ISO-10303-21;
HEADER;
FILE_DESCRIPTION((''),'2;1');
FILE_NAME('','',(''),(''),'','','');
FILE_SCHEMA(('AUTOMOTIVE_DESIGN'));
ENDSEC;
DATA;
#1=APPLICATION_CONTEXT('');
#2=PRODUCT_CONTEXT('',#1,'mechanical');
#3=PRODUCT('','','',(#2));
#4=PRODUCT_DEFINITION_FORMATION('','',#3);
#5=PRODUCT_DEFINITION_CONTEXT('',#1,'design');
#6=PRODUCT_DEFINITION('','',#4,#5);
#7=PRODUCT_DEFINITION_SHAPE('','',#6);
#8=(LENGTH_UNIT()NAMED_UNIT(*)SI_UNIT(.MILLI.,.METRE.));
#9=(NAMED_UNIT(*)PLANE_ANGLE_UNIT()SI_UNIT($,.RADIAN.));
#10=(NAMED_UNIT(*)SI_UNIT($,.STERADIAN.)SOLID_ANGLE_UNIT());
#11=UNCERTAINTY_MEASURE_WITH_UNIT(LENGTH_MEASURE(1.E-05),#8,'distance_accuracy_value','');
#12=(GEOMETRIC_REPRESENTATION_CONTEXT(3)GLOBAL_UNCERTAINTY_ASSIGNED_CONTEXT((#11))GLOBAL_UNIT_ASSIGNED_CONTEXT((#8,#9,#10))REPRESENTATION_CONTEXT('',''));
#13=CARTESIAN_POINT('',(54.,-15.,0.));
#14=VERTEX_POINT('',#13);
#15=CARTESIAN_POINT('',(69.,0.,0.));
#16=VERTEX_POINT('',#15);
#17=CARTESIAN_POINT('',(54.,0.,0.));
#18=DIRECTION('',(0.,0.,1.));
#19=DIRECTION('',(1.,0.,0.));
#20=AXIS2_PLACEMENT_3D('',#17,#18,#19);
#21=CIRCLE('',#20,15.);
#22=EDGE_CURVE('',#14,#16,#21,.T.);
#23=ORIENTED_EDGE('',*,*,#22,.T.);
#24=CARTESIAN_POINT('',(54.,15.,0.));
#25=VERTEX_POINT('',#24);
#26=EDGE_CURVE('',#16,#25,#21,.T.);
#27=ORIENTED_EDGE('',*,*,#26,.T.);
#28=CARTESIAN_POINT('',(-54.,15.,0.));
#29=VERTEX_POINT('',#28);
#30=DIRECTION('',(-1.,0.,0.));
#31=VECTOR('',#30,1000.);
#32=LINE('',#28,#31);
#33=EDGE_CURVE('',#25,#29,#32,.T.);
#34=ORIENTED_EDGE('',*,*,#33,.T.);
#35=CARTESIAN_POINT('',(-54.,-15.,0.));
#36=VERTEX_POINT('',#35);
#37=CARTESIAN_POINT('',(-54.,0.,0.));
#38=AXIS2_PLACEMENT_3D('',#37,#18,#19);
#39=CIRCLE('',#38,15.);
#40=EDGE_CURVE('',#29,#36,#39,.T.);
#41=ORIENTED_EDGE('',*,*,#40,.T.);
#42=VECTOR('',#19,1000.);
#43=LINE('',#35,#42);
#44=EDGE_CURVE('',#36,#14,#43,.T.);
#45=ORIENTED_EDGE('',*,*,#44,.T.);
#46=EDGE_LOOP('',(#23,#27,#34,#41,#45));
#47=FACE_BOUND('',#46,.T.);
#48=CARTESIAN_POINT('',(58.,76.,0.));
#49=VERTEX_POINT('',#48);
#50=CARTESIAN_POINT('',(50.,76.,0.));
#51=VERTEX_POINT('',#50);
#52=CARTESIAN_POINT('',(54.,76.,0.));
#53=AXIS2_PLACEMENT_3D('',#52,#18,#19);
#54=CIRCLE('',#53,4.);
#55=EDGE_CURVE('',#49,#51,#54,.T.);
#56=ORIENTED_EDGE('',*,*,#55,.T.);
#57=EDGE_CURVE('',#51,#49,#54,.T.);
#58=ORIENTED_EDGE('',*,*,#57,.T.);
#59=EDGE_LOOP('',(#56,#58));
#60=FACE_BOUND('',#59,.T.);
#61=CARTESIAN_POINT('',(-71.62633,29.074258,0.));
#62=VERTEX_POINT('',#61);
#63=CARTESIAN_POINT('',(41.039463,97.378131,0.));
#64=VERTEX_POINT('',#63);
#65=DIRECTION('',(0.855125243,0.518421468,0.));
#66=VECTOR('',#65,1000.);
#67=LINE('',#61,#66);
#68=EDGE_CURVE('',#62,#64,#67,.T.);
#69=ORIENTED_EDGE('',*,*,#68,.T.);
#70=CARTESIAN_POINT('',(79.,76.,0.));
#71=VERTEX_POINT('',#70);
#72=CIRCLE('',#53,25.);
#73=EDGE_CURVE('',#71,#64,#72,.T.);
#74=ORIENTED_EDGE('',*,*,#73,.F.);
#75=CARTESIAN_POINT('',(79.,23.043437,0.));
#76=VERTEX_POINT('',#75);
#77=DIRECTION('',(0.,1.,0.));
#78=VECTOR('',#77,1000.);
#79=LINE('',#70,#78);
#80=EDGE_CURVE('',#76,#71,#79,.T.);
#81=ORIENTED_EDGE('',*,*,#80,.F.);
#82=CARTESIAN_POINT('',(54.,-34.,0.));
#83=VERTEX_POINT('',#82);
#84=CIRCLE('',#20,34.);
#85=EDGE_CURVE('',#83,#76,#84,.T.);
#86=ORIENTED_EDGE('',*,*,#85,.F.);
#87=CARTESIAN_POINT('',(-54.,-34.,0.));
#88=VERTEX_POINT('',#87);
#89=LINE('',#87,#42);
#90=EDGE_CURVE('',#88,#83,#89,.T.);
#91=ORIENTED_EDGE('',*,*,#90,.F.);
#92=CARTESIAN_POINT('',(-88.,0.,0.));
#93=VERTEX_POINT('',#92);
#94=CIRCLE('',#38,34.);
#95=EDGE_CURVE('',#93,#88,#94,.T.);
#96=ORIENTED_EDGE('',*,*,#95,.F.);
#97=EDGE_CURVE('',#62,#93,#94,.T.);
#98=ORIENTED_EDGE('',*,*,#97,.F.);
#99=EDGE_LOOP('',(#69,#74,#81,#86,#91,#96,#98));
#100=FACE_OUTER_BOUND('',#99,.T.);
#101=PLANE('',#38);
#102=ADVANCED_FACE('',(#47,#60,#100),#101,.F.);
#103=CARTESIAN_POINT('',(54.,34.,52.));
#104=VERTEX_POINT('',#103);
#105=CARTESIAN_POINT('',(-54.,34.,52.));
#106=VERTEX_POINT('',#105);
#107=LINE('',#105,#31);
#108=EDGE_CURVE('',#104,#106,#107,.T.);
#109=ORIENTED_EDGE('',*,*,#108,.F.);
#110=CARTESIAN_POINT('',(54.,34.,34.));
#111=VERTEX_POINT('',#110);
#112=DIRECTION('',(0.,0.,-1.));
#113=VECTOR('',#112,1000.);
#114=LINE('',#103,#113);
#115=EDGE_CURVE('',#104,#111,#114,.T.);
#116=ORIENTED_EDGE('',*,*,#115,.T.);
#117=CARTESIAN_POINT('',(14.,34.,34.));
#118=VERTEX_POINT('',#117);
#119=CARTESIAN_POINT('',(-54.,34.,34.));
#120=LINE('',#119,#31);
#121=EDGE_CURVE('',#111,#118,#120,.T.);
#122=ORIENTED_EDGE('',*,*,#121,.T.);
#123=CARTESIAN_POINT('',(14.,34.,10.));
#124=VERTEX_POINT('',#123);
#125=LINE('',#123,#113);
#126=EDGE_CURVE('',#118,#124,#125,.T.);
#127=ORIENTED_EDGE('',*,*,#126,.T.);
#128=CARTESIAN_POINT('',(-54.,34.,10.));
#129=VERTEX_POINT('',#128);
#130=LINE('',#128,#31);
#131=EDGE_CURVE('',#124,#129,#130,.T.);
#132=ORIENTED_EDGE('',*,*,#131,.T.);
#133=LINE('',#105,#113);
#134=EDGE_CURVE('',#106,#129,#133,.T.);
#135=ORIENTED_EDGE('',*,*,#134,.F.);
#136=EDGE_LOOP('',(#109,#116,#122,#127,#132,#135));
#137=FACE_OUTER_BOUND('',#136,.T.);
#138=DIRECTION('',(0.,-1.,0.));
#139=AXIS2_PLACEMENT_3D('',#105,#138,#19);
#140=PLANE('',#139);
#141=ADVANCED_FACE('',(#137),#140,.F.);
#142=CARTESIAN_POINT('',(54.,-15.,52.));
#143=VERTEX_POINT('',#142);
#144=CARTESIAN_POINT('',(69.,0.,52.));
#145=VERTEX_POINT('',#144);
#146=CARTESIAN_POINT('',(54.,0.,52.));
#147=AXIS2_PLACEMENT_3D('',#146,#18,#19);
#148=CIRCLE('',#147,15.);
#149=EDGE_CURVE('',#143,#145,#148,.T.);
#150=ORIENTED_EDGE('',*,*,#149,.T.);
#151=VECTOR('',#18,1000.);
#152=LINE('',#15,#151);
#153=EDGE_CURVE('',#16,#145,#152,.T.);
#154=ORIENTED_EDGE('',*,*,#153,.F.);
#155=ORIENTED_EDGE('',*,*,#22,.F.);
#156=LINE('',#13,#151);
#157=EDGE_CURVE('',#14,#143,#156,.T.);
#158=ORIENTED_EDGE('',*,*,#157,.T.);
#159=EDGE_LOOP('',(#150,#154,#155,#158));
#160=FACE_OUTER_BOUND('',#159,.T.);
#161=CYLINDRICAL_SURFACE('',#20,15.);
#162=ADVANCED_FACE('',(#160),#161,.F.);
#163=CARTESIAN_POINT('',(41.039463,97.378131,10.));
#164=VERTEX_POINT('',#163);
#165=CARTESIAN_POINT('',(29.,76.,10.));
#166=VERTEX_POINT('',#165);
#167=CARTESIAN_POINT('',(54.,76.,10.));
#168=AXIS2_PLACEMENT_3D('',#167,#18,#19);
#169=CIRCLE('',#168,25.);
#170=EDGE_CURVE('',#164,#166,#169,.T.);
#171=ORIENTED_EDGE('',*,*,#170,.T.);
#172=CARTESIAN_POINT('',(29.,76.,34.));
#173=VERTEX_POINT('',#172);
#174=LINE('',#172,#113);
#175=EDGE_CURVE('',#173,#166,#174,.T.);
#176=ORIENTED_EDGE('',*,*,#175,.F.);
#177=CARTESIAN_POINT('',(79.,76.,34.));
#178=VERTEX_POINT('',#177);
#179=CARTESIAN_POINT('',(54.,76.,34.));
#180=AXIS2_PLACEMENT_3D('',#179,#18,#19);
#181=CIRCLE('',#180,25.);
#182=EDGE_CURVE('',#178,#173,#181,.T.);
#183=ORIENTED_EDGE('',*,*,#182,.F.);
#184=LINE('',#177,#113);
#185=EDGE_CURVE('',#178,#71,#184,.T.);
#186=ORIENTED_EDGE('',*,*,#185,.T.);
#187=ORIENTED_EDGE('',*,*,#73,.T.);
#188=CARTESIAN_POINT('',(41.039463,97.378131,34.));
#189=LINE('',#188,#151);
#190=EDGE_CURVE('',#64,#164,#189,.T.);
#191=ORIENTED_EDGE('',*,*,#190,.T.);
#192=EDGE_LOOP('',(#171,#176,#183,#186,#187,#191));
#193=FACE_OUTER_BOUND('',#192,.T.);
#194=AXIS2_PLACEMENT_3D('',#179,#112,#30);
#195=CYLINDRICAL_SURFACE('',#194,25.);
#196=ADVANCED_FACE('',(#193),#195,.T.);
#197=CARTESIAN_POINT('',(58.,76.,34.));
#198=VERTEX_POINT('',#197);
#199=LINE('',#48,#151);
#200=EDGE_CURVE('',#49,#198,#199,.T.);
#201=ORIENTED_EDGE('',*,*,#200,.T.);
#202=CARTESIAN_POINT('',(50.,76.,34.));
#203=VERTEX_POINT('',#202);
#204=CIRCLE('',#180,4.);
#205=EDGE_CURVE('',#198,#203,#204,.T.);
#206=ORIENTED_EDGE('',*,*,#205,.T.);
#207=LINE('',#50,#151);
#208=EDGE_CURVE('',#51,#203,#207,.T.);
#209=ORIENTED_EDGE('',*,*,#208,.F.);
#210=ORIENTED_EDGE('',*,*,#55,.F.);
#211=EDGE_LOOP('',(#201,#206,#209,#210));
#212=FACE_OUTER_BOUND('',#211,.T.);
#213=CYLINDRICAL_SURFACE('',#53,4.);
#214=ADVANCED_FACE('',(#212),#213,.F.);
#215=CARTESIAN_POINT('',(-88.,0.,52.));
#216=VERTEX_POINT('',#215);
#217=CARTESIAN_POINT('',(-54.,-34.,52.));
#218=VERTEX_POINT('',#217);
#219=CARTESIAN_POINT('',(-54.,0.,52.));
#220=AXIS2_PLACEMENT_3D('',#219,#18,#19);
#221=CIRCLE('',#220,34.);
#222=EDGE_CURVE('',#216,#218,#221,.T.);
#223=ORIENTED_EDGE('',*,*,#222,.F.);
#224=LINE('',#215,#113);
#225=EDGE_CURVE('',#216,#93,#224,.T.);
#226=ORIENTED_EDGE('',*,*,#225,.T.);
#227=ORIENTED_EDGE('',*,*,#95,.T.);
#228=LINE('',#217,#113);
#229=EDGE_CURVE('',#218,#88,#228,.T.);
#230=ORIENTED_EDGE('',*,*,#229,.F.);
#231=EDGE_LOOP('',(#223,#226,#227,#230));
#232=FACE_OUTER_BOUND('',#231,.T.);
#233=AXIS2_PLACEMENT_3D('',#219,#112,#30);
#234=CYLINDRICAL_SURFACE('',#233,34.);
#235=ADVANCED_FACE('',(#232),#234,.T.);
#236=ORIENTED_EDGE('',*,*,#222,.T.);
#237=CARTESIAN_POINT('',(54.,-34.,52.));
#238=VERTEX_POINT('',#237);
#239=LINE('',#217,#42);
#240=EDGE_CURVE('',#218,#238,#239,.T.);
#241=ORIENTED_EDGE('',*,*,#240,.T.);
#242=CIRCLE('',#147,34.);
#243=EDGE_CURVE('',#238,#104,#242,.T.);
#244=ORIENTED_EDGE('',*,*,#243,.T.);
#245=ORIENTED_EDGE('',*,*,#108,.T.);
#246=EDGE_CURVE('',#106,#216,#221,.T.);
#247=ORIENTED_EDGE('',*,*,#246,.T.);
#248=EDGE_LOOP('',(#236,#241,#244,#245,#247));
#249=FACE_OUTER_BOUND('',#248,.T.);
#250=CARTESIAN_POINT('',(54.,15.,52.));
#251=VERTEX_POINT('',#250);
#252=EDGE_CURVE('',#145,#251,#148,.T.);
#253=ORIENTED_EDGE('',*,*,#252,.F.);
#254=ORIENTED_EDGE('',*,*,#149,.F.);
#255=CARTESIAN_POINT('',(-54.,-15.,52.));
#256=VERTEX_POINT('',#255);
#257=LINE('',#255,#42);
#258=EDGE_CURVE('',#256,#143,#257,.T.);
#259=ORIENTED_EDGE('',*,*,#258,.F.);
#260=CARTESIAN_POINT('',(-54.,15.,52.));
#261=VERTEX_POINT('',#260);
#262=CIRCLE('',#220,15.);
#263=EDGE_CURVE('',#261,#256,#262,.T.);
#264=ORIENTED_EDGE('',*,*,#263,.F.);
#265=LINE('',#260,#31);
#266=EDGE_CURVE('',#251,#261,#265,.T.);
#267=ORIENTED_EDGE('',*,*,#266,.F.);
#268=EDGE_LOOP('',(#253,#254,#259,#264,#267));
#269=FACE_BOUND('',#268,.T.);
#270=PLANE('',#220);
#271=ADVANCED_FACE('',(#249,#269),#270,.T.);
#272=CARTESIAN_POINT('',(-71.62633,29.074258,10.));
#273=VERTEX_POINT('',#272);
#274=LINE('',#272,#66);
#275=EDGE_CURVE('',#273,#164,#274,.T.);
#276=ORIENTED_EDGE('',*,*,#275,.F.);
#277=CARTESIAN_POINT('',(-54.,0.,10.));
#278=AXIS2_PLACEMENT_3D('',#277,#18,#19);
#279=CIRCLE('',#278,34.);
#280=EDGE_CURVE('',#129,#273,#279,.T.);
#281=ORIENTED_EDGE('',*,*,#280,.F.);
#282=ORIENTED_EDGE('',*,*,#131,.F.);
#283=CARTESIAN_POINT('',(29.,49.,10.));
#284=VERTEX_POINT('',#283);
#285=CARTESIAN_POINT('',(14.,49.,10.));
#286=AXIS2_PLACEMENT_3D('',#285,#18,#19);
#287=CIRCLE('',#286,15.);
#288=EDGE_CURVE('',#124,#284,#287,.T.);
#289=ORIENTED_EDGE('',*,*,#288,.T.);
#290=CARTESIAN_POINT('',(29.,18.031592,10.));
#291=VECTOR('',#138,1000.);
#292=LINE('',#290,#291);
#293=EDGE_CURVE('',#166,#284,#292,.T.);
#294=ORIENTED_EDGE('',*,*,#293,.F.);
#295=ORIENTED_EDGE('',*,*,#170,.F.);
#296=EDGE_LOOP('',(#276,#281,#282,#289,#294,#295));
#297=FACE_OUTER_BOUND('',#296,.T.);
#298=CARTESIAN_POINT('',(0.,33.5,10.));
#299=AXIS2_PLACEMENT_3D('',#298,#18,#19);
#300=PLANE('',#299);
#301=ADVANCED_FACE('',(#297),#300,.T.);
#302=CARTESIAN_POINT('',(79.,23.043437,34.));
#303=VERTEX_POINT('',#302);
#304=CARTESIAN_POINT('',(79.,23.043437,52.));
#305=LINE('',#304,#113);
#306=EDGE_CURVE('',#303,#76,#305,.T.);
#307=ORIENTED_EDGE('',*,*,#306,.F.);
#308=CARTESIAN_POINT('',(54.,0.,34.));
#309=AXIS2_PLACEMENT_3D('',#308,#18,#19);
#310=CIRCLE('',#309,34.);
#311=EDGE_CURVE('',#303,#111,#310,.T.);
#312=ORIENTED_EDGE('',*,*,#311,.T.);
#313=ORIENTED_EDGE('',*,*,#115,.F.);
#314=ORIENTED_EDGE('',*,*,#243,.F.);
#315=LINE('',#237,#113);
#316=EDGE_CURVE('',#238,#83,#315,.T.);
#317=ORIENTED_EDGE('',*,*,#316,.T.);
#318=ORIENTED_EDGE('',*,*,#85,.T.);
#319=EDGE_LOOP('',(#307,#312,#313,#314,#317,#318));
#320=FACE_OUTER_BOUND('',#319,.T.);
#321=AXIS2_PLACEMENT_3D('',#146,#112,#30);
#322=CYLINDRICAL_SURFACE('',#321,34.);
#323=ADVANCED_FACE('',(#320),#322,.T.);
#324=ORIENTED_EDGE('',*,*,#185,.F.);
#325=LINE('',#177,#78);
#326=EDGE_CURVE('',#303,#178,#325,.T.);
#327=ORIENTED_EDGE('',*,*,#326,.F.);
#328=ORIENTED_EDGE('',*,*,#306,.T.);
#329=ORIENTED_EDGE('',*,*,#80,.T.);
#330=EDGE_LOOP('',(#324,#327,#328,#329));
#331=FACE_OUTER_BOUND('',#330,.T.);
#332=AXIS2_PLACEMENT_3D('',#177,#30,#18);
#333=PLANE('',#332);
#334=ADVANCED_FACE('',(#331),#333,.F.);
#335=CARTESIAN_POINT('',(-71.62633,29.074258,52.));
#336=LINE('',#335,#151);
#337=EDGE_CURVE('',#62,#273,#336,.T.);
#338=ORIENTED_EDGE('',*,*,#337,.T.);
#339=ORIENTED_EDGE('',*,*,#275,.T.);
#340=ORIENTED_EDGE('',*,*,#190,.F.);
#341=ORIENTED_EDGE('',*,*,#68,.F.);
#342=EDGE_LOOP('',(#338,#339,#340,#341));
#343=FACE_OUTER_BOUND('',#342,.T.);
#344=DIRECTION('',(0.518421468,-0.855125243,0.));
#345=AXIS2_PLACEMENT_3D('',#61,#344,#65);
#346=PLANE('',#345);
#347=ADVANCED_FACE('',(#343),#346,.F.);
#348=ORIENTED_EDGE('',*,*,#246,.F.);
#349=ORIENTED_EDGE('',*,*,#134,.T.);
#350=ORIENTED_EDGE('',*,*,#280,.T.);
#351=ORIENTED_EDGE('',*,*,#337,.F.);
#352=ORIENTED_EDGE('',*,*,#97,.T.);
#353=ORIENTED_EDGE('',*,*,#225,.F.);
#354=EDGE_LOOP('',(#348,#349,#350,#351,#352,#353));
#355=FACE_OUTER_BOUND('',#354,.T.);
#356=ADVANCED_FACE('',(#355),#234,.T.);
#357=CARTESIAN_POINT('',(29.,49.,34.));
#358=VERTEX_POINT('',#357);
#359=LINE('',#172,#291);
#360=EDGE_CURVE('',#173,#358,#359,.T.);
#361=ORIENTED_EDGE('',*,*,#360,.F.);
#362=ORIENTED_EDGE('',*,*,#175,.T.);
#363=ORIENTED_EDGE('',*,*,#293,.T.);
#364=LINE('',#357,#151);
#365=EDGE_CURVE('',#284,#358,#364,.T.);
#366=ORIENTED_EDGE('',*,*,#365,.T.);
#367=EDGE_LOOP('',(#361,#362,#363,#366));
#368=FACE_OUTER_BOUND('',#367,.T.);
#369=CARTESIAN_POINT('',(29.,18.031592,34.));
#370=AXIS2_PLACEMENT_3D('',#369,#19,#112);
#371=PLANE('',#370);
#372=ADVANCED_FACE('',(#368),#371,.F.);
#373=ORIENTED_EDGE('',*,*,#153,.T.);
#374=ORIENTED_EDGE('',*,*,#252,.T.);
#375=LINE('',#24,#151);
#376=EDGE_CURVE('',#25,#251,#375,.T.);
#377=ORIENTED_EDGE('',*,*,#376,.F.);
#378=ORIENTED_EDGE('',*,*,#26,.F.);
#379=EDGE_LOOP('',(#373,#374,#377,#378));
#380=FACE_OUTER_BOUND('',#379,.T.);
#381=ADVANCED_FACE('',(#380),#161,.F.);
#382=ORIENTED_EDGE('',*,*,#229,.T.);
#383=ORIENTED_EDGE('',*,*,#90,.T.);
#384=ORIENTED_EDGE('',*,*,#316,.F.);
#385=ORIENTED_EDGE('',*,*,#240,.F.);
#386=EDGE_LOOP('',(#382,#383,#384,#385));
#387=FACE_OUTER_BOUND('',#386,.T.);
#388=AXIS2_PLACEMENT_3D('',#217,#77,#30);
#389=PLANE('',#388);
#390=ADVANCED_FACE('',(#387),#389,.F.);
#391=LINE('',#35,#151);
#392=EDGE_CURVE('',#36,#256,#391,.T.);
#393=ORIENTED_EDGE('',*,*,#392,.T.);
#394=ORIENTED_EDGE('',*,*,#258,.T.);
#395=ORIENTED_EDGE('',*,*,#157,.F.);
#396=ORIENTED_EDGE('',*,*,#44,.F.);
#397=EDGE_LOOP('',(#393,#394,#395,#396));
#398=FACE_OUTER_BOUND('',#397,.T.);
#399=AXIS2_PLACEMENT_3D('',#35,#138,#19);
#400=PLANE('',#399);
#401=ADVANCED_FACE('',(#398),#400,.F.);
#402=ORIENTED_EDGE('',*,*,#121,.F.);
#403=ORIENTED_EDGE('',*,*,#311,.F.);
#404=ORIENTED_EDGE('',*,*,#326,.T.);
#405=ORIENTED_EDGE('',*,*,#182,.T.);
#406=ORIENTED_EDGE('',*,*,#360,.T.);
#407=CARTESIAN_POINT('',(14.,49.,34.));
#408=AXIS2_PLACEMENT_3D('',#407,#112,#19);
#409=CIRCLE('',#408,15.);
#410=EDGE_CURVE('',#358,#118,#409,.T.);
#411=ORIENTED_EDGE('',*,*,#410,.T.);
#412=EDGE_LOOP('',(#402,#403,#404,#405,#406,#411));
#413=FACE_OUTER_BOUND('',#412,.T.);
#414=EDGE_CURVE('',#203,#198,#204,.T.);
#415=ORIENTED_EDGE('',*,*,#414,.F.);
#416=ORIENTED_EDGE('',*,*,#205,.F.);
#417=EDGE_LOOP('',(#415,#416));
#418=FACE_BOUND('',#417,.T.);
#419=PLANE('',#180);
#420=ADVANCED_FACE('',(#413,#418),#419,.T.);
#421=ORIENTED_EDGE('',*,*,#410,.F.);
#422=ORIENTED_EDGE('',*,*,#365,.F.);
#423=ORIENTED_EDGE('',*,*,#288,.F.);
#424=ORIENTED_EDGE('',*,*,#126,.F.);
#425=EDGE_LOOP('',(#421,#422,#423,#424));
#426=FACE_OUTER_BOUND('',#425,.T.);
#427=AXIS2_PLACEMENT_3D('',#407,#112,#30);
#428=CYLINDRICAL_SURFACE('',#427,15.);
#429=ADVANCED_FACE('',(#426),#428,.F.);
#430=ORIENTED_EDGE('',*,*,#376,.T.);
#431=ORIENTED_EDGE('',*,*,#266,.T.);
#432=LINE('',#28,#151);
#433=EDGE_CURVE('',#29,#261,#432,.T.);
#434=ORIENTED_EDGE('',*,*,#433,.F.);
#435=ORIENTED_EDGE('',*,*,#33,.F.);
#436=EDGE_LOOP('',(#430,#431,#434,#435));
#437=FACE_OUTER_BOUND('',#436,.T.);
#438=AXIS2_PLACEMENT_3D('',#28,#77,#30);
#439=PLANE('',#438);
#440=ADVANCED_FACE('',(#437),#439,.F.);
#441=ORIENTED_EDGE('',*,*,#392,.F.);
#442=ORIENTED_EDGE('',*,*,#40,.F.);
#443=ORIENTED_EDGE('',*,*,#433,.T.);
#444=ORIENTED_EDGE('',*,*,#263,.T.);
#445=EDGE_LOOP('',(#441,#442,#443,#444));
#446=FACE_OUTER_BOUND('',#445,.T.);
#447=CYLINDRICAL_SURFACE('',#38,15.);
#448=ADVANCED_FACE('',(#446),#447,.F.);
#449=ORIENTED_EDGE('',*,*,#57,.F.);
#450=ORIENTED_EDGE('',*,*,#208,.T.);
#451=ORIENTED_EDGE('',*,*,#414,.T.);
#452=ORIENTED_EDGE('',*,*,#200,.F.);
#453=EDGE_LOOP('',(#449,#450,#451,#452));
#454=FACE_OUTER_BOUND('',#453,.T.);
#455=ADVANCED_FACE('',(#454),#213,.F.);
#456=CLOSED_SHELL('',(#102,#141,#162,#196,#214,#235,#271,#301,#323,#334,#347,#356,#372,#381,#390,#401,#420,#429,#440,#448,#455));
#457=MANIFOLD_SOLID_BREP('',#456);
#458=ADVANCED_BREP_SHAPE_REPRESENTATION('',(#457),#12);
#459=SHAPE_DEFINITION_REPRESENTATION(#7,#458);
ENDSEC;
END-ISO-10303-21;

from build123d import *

# Parameters (mm, degrees)
LINK_PLATE_DEPTH          = 52
LINK_SLOT_DEPTH           = 52
PIVOT_BOSS_DEPTH          = 34
PIVOT_PIN_HOLE_SKETCH_R   = 4
PIVOT_PIN_HOLE_DEPTH      = 34
SUPPORT_RIB_10MM_REACH    = 145.698
SUPPORT_RIB_SKETCH_WALL_W = 421.148756116
SUPPORT_RIB_SKETCH_WALL_H = 10
EDGE_FILLETS_R15_R        = 15


with BuildPart() as part:
    # Link Plate Outline Sketch → Link Plate (new body)
    with BuildSketch(Plane.XY):
        with BuildLine():
            Line((-54, 34), (54, 34))
            ThreePointArc((54, 34), (88, 0), (54, -34))
            Line((54, -34), (-54, -34))
            ThreePointArc((-54, -34), (-88, 0), (-54, 34))
        make_face()
    extrude(amount=LINK_PLATE_DEPTH)

    # Link Slot Sketch → Link Slot (cut)
    with BuildSketch(Plane.XY.offset(52)):
        with BuildLine():
            Line((-54, 15), (54, 15))
            ThreePointArc((54, 15), (69, 0), (54, -15))
            Line((54, -15), (-54, -15))
            ThreePointArc((-54, -15), (-69, 0), (-54, 15))
        make_face()
    extrude(amount=-LINK_SLOT_DEPTH, mode=Mode.SUBTRACT)

    # Pivot Boss Sketch → Pivot Boss (add)
    with BuildSketch(Plane.XY):
        with BuildLine():
            Line((29, 76), (29, 34))
            Line((29, 34), (29, 18.031591918))
            Line((29, 18.031591918), (79, 18.031591918))
            Line((79, 18.031591918), (79, 76))
            ThreePointArc((79, 76), (54, 101), (29, 76))
        make_face()
    extrude(amount=PIVOT_BOSS_DEPTH)

    # Pivot Pin Hole Sketch → Pivot Pin Hole (cut)
    with BuildSketch(Plane.XY.offset(34)):
        with Locations((54, 76)):
            Circle(PIVOT_PIN_HOLE_SKETCH_R)
    extrude(amount=-PIVOT_PIN_HOLE_DEPTH, mode=Mode.SUBTRACT)

    # Support Rib Sketch wall → Support Rib 10mm (add, up to next)
    with BuildSketch(Plane(origin=(-15.293433294, 63.226194681, 0), x_dir=(0.855125243419, 0.518421467599, 0), z_dir=(-0.518421467599, 0.855125243419, 0)), mode=Mode.PRIVATE) as support_rib_10mm_sk1:
        with Locations((0, -5)):
            Rectangle(SUPPORT_RIB_SKETCH_WALL_W, SUPPORT_RIB_SKETCH_WALL_H)
    support_rib_10mm_tool1 = extrude(support_rib_10mm_sk1.sketch, amount=-SUPPORT_RIB_10MM_REACH, mode=Mode.PRIVATE) - part.part
    add(support_rib_10mm_tool1.solids().sort_by_distance((-15.293433294, 63.226194681, 0))[0])

    # Edge Fillets R15
    edge_fillets_r15_edges = [part.edges().sort_by_distance(p)[0] for p in [
        (29, 34, 22),
    ]]
    fillet(edge_fillets_r15_edges, radius=EDGE_FILLETS_R15_R)


solid = part.part
